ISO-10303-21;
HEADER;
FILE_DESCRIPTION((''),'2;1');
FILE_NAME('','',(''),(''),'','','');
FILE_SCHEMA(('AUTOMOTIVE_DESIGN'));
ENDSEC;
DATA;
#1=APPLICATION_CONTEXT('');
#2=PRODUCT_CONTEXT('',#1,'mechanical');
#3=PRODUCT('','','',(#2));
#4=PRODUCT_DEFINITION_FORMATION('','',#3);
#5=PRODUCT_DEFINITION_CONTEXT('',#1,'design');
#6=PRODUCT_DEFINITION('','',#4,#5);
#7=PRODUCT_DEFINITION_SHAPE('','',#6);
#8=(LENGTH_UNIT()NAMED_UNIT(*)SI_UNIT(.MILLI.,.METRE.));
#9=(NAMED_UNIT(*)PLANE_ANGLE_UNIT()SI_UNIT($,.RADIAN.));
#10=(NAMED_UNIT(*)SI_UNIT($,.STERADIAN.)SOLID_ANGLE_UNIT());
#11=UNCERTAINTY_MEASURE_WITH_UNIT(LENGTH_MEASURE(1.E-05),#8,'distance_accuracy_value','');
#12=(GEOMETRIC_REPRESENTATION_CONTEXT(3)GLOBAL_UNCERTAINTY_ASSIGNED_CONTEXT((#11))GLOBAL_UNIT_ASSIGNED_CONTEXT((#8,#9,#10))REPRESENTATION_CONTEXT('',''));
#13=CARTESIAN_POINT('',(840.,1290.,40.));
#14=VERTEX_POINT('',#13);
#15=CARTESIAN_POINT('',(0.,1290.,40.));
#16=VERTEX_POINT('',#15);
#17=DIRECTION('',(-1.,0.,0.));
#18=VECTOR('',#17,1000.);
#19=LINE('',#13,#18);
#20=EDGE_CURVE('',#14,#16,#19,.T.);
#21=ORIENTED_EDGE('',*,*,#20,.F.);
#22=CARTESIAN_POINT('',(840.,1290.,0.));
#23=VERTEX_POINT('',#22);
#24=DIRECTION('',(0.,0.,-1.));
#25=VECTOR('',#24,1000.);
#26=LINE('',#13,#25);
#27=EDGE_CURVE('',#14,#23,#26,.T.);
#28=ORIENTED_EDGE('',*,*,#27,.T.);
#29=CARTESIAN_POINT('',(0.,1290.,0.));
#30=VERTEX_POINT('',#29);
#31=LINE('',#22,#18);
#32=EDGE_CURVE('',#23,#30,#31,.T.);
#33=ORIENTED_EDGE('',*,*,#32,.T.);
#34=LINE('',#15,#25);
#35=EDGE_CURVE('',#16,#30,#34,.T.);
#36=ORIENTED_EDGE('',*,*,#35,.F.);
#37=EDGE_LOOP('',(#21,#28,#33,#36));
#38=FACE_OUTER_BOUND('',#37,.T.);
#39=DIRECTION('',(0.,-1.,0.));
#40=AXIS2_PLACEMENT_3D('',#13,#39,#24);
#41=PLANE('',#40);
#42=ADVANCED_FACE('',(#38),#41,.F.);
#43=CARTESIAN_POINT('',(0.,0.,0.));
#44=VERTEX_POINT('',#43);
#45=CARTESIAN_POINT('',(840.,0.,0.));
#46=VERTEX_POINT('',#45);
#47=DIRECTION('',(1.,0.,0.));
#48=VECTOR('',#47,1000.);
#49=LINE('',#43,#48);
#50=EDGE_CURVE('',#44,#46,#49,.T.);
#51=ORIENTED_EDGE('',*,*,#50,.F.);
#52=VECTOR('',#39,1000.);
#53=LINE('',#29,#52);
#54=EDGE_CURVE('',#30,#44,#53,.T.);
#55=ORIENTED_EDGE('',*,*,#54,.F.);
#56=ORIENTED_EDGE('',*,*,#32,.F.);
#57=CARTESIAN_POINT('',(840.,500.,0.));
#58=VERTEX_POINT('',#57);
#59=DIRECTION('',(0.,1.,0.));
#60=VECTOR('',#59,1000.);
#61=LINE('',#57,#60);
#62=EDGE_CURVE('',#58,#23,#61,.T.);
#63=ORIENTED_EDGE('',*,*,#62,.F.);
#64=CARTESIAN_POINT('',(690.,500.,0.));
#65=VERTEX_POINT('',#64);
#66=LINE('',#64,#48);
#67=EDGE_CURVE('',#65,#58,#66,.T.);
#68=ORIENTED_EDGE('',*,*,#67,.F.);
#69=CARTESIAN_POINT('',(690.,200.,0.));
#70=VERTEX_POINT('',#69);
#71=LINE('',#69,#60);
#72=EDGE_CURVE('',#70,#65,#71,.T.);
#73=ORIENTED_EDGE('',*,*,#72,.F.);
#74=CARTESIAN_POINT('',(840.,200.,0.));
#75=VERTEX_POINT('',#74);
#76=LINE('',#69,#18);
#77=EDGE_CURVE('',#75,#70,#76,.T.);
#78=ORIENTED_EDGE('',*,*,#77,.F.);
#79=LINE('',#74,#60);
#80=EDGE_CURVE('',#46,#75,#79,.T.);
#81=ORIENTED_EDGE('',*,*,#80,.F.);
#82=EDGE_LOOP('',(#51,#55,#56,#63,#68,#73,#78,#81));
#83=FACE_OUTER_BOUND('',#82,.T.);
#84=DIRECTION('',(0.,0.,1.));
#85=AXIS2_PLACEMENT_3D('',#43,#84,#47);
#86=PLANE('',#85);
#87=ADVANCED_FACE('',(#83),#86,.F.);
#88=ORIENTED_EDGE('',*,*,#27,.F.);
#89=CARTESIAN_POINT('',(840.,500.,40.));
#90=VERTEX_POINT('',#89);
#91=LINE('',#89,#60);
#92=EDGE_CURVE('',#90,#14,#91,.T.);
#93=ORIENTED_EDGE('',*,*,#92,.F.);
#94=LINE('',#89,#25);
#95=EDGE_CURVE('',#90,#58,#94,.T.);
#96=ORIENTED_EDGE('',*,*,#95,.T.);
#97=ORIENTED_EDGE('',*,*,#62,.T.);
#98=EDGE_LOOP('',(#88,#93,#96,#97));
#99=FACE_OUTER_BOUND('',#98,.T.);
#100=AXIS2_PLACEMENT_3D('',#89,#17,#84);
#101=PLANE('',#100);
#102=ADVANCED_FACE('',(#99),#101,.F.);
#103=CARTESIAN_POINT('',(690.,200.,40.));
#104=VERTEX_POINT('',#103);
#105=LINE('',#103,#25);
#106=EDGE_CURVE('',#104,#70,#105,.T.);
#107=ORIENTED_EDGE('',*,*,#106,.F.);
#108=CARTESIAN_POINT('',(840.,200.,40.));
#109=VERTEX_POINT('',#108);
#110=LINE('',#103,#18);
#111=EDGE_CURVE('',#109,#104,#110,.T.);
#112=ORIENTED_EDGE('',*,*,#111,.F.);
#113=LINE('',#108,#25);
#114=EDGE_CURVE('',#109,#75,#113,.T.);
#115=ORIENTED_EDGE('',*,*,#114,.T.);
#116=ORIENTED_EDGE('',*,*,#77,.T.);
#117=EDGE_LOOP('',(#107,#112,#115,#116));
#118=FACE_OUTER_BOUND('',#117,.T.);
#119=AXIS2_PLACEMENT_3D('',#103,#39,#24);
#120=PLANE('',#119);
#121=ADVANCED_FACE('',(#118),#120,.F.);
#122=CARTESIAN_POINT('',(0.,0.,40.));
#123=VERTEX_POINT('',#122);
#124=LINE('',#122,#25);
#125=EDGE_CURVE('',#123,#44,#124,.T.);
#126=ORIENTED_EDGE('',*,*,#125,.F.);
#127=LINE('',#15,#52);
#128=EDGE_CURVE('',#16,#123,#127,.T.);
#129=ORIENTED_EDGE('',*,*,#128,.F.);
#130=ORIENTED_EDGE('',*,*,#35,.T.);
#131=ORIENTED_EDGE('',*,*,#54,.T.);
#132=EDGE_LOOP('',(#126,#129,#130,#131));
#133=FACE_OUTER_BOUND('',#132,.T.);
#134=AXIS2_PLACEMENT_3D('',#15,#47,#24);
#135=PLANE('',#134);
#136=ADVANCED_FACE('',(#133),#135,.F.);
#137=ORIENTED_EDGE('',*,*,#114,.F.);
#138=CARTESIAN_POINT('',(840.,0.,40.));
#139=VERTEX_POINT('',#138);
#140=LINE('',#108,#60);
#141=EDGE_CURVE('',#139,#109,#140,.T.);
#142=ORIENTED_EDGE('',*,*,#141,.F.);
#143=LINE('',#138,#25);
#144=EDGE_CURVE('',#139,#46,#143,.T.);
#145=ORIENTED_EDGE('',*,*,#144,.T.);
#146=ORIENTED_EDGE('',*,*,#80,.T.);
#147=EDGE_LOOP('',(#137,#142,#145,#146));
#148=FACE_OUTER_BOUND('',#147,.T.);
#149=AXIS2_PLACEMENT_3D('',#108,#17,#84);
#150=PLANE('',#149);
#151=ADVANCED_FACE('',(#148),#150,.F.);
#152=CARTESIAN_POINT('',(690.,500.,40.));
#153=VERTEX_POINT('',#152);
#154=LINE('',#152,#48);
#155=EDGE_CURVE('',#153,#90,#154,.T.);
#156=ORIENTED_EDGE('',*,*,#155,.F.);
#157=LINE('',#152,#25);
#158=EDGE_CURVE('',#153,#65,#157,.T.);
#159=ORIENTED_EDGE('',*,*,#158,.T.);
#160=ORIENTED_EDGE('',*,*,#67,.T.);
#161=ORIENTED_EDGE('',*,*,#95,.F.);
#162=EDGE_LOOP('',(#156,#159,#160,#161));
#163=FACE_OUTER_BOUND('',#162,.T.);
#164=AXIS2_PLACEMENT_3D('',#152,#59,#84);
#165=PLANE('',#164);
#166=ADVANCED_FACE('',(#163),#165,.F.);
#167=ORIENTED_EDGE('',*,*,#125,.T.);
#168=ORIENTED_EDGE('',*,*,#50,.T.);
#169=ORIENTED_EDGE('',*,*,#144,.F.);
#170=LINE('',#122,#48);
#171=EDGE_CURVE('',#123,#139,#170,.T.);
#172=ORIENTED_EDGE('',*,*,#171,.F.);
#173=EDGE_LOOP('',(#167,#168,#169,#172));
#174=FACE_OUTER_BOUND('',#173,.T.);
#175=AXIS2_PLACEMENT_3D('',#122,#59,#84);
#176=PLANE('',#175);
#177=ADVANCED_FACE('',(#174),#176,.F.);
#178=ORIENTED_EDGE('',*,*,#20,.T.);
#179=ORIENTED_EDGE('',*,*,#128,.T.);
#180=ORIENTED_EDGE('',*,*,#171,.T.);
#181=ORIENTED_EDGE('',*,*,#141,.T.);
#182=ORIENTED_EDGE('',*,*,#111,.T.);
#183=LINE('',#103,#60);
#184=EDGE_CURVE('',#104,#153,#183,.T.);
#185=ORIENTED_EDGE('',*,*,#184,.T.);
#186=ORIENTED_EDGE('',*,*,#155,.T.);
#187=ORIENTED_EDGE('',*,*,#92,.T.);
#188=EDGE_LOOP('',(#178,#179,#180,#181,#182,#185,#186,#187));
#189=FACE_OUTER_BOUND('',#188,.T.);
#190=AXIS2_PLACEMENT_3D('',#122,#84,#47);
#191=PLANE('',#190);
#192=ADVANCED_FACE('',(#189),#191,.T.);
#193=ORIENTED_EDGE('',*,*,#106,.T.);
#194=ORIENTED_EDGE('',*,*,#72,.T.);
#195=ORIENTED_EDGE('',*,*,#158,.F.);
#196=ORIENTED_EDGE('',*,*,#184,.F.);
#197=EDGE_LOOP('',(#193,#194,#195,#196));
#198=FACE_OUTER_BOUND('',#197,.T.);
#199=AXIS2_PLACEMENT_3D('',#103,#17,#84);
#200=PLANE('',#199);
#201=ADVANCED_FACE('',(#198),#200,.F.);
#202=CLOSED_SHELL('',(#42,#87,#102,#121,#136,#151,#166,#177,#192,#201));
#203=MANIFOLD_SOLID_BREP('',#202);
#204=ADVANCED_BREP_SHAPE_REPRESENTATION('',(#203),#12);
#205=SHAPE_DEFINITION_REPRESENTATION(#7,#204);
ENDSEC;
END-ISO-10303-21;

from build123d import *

# Parameters (mm, degrees)
BOSS_EXTRUDE1_DEPTH = 40


with BuildPart() as part:
    # Sketch1 → Boss-Extrude1 (new body)
    with BuildSketch(Plane.XY):
        Polygon((0, 0), (840, 0), (840, 200), (690, 200), (690, 500), (840, 500), (840, 1290), (0, 1290), align=None)
    extrude(amount=BOSS_EXTRUDE1_DEPTH)


solid = part.part
